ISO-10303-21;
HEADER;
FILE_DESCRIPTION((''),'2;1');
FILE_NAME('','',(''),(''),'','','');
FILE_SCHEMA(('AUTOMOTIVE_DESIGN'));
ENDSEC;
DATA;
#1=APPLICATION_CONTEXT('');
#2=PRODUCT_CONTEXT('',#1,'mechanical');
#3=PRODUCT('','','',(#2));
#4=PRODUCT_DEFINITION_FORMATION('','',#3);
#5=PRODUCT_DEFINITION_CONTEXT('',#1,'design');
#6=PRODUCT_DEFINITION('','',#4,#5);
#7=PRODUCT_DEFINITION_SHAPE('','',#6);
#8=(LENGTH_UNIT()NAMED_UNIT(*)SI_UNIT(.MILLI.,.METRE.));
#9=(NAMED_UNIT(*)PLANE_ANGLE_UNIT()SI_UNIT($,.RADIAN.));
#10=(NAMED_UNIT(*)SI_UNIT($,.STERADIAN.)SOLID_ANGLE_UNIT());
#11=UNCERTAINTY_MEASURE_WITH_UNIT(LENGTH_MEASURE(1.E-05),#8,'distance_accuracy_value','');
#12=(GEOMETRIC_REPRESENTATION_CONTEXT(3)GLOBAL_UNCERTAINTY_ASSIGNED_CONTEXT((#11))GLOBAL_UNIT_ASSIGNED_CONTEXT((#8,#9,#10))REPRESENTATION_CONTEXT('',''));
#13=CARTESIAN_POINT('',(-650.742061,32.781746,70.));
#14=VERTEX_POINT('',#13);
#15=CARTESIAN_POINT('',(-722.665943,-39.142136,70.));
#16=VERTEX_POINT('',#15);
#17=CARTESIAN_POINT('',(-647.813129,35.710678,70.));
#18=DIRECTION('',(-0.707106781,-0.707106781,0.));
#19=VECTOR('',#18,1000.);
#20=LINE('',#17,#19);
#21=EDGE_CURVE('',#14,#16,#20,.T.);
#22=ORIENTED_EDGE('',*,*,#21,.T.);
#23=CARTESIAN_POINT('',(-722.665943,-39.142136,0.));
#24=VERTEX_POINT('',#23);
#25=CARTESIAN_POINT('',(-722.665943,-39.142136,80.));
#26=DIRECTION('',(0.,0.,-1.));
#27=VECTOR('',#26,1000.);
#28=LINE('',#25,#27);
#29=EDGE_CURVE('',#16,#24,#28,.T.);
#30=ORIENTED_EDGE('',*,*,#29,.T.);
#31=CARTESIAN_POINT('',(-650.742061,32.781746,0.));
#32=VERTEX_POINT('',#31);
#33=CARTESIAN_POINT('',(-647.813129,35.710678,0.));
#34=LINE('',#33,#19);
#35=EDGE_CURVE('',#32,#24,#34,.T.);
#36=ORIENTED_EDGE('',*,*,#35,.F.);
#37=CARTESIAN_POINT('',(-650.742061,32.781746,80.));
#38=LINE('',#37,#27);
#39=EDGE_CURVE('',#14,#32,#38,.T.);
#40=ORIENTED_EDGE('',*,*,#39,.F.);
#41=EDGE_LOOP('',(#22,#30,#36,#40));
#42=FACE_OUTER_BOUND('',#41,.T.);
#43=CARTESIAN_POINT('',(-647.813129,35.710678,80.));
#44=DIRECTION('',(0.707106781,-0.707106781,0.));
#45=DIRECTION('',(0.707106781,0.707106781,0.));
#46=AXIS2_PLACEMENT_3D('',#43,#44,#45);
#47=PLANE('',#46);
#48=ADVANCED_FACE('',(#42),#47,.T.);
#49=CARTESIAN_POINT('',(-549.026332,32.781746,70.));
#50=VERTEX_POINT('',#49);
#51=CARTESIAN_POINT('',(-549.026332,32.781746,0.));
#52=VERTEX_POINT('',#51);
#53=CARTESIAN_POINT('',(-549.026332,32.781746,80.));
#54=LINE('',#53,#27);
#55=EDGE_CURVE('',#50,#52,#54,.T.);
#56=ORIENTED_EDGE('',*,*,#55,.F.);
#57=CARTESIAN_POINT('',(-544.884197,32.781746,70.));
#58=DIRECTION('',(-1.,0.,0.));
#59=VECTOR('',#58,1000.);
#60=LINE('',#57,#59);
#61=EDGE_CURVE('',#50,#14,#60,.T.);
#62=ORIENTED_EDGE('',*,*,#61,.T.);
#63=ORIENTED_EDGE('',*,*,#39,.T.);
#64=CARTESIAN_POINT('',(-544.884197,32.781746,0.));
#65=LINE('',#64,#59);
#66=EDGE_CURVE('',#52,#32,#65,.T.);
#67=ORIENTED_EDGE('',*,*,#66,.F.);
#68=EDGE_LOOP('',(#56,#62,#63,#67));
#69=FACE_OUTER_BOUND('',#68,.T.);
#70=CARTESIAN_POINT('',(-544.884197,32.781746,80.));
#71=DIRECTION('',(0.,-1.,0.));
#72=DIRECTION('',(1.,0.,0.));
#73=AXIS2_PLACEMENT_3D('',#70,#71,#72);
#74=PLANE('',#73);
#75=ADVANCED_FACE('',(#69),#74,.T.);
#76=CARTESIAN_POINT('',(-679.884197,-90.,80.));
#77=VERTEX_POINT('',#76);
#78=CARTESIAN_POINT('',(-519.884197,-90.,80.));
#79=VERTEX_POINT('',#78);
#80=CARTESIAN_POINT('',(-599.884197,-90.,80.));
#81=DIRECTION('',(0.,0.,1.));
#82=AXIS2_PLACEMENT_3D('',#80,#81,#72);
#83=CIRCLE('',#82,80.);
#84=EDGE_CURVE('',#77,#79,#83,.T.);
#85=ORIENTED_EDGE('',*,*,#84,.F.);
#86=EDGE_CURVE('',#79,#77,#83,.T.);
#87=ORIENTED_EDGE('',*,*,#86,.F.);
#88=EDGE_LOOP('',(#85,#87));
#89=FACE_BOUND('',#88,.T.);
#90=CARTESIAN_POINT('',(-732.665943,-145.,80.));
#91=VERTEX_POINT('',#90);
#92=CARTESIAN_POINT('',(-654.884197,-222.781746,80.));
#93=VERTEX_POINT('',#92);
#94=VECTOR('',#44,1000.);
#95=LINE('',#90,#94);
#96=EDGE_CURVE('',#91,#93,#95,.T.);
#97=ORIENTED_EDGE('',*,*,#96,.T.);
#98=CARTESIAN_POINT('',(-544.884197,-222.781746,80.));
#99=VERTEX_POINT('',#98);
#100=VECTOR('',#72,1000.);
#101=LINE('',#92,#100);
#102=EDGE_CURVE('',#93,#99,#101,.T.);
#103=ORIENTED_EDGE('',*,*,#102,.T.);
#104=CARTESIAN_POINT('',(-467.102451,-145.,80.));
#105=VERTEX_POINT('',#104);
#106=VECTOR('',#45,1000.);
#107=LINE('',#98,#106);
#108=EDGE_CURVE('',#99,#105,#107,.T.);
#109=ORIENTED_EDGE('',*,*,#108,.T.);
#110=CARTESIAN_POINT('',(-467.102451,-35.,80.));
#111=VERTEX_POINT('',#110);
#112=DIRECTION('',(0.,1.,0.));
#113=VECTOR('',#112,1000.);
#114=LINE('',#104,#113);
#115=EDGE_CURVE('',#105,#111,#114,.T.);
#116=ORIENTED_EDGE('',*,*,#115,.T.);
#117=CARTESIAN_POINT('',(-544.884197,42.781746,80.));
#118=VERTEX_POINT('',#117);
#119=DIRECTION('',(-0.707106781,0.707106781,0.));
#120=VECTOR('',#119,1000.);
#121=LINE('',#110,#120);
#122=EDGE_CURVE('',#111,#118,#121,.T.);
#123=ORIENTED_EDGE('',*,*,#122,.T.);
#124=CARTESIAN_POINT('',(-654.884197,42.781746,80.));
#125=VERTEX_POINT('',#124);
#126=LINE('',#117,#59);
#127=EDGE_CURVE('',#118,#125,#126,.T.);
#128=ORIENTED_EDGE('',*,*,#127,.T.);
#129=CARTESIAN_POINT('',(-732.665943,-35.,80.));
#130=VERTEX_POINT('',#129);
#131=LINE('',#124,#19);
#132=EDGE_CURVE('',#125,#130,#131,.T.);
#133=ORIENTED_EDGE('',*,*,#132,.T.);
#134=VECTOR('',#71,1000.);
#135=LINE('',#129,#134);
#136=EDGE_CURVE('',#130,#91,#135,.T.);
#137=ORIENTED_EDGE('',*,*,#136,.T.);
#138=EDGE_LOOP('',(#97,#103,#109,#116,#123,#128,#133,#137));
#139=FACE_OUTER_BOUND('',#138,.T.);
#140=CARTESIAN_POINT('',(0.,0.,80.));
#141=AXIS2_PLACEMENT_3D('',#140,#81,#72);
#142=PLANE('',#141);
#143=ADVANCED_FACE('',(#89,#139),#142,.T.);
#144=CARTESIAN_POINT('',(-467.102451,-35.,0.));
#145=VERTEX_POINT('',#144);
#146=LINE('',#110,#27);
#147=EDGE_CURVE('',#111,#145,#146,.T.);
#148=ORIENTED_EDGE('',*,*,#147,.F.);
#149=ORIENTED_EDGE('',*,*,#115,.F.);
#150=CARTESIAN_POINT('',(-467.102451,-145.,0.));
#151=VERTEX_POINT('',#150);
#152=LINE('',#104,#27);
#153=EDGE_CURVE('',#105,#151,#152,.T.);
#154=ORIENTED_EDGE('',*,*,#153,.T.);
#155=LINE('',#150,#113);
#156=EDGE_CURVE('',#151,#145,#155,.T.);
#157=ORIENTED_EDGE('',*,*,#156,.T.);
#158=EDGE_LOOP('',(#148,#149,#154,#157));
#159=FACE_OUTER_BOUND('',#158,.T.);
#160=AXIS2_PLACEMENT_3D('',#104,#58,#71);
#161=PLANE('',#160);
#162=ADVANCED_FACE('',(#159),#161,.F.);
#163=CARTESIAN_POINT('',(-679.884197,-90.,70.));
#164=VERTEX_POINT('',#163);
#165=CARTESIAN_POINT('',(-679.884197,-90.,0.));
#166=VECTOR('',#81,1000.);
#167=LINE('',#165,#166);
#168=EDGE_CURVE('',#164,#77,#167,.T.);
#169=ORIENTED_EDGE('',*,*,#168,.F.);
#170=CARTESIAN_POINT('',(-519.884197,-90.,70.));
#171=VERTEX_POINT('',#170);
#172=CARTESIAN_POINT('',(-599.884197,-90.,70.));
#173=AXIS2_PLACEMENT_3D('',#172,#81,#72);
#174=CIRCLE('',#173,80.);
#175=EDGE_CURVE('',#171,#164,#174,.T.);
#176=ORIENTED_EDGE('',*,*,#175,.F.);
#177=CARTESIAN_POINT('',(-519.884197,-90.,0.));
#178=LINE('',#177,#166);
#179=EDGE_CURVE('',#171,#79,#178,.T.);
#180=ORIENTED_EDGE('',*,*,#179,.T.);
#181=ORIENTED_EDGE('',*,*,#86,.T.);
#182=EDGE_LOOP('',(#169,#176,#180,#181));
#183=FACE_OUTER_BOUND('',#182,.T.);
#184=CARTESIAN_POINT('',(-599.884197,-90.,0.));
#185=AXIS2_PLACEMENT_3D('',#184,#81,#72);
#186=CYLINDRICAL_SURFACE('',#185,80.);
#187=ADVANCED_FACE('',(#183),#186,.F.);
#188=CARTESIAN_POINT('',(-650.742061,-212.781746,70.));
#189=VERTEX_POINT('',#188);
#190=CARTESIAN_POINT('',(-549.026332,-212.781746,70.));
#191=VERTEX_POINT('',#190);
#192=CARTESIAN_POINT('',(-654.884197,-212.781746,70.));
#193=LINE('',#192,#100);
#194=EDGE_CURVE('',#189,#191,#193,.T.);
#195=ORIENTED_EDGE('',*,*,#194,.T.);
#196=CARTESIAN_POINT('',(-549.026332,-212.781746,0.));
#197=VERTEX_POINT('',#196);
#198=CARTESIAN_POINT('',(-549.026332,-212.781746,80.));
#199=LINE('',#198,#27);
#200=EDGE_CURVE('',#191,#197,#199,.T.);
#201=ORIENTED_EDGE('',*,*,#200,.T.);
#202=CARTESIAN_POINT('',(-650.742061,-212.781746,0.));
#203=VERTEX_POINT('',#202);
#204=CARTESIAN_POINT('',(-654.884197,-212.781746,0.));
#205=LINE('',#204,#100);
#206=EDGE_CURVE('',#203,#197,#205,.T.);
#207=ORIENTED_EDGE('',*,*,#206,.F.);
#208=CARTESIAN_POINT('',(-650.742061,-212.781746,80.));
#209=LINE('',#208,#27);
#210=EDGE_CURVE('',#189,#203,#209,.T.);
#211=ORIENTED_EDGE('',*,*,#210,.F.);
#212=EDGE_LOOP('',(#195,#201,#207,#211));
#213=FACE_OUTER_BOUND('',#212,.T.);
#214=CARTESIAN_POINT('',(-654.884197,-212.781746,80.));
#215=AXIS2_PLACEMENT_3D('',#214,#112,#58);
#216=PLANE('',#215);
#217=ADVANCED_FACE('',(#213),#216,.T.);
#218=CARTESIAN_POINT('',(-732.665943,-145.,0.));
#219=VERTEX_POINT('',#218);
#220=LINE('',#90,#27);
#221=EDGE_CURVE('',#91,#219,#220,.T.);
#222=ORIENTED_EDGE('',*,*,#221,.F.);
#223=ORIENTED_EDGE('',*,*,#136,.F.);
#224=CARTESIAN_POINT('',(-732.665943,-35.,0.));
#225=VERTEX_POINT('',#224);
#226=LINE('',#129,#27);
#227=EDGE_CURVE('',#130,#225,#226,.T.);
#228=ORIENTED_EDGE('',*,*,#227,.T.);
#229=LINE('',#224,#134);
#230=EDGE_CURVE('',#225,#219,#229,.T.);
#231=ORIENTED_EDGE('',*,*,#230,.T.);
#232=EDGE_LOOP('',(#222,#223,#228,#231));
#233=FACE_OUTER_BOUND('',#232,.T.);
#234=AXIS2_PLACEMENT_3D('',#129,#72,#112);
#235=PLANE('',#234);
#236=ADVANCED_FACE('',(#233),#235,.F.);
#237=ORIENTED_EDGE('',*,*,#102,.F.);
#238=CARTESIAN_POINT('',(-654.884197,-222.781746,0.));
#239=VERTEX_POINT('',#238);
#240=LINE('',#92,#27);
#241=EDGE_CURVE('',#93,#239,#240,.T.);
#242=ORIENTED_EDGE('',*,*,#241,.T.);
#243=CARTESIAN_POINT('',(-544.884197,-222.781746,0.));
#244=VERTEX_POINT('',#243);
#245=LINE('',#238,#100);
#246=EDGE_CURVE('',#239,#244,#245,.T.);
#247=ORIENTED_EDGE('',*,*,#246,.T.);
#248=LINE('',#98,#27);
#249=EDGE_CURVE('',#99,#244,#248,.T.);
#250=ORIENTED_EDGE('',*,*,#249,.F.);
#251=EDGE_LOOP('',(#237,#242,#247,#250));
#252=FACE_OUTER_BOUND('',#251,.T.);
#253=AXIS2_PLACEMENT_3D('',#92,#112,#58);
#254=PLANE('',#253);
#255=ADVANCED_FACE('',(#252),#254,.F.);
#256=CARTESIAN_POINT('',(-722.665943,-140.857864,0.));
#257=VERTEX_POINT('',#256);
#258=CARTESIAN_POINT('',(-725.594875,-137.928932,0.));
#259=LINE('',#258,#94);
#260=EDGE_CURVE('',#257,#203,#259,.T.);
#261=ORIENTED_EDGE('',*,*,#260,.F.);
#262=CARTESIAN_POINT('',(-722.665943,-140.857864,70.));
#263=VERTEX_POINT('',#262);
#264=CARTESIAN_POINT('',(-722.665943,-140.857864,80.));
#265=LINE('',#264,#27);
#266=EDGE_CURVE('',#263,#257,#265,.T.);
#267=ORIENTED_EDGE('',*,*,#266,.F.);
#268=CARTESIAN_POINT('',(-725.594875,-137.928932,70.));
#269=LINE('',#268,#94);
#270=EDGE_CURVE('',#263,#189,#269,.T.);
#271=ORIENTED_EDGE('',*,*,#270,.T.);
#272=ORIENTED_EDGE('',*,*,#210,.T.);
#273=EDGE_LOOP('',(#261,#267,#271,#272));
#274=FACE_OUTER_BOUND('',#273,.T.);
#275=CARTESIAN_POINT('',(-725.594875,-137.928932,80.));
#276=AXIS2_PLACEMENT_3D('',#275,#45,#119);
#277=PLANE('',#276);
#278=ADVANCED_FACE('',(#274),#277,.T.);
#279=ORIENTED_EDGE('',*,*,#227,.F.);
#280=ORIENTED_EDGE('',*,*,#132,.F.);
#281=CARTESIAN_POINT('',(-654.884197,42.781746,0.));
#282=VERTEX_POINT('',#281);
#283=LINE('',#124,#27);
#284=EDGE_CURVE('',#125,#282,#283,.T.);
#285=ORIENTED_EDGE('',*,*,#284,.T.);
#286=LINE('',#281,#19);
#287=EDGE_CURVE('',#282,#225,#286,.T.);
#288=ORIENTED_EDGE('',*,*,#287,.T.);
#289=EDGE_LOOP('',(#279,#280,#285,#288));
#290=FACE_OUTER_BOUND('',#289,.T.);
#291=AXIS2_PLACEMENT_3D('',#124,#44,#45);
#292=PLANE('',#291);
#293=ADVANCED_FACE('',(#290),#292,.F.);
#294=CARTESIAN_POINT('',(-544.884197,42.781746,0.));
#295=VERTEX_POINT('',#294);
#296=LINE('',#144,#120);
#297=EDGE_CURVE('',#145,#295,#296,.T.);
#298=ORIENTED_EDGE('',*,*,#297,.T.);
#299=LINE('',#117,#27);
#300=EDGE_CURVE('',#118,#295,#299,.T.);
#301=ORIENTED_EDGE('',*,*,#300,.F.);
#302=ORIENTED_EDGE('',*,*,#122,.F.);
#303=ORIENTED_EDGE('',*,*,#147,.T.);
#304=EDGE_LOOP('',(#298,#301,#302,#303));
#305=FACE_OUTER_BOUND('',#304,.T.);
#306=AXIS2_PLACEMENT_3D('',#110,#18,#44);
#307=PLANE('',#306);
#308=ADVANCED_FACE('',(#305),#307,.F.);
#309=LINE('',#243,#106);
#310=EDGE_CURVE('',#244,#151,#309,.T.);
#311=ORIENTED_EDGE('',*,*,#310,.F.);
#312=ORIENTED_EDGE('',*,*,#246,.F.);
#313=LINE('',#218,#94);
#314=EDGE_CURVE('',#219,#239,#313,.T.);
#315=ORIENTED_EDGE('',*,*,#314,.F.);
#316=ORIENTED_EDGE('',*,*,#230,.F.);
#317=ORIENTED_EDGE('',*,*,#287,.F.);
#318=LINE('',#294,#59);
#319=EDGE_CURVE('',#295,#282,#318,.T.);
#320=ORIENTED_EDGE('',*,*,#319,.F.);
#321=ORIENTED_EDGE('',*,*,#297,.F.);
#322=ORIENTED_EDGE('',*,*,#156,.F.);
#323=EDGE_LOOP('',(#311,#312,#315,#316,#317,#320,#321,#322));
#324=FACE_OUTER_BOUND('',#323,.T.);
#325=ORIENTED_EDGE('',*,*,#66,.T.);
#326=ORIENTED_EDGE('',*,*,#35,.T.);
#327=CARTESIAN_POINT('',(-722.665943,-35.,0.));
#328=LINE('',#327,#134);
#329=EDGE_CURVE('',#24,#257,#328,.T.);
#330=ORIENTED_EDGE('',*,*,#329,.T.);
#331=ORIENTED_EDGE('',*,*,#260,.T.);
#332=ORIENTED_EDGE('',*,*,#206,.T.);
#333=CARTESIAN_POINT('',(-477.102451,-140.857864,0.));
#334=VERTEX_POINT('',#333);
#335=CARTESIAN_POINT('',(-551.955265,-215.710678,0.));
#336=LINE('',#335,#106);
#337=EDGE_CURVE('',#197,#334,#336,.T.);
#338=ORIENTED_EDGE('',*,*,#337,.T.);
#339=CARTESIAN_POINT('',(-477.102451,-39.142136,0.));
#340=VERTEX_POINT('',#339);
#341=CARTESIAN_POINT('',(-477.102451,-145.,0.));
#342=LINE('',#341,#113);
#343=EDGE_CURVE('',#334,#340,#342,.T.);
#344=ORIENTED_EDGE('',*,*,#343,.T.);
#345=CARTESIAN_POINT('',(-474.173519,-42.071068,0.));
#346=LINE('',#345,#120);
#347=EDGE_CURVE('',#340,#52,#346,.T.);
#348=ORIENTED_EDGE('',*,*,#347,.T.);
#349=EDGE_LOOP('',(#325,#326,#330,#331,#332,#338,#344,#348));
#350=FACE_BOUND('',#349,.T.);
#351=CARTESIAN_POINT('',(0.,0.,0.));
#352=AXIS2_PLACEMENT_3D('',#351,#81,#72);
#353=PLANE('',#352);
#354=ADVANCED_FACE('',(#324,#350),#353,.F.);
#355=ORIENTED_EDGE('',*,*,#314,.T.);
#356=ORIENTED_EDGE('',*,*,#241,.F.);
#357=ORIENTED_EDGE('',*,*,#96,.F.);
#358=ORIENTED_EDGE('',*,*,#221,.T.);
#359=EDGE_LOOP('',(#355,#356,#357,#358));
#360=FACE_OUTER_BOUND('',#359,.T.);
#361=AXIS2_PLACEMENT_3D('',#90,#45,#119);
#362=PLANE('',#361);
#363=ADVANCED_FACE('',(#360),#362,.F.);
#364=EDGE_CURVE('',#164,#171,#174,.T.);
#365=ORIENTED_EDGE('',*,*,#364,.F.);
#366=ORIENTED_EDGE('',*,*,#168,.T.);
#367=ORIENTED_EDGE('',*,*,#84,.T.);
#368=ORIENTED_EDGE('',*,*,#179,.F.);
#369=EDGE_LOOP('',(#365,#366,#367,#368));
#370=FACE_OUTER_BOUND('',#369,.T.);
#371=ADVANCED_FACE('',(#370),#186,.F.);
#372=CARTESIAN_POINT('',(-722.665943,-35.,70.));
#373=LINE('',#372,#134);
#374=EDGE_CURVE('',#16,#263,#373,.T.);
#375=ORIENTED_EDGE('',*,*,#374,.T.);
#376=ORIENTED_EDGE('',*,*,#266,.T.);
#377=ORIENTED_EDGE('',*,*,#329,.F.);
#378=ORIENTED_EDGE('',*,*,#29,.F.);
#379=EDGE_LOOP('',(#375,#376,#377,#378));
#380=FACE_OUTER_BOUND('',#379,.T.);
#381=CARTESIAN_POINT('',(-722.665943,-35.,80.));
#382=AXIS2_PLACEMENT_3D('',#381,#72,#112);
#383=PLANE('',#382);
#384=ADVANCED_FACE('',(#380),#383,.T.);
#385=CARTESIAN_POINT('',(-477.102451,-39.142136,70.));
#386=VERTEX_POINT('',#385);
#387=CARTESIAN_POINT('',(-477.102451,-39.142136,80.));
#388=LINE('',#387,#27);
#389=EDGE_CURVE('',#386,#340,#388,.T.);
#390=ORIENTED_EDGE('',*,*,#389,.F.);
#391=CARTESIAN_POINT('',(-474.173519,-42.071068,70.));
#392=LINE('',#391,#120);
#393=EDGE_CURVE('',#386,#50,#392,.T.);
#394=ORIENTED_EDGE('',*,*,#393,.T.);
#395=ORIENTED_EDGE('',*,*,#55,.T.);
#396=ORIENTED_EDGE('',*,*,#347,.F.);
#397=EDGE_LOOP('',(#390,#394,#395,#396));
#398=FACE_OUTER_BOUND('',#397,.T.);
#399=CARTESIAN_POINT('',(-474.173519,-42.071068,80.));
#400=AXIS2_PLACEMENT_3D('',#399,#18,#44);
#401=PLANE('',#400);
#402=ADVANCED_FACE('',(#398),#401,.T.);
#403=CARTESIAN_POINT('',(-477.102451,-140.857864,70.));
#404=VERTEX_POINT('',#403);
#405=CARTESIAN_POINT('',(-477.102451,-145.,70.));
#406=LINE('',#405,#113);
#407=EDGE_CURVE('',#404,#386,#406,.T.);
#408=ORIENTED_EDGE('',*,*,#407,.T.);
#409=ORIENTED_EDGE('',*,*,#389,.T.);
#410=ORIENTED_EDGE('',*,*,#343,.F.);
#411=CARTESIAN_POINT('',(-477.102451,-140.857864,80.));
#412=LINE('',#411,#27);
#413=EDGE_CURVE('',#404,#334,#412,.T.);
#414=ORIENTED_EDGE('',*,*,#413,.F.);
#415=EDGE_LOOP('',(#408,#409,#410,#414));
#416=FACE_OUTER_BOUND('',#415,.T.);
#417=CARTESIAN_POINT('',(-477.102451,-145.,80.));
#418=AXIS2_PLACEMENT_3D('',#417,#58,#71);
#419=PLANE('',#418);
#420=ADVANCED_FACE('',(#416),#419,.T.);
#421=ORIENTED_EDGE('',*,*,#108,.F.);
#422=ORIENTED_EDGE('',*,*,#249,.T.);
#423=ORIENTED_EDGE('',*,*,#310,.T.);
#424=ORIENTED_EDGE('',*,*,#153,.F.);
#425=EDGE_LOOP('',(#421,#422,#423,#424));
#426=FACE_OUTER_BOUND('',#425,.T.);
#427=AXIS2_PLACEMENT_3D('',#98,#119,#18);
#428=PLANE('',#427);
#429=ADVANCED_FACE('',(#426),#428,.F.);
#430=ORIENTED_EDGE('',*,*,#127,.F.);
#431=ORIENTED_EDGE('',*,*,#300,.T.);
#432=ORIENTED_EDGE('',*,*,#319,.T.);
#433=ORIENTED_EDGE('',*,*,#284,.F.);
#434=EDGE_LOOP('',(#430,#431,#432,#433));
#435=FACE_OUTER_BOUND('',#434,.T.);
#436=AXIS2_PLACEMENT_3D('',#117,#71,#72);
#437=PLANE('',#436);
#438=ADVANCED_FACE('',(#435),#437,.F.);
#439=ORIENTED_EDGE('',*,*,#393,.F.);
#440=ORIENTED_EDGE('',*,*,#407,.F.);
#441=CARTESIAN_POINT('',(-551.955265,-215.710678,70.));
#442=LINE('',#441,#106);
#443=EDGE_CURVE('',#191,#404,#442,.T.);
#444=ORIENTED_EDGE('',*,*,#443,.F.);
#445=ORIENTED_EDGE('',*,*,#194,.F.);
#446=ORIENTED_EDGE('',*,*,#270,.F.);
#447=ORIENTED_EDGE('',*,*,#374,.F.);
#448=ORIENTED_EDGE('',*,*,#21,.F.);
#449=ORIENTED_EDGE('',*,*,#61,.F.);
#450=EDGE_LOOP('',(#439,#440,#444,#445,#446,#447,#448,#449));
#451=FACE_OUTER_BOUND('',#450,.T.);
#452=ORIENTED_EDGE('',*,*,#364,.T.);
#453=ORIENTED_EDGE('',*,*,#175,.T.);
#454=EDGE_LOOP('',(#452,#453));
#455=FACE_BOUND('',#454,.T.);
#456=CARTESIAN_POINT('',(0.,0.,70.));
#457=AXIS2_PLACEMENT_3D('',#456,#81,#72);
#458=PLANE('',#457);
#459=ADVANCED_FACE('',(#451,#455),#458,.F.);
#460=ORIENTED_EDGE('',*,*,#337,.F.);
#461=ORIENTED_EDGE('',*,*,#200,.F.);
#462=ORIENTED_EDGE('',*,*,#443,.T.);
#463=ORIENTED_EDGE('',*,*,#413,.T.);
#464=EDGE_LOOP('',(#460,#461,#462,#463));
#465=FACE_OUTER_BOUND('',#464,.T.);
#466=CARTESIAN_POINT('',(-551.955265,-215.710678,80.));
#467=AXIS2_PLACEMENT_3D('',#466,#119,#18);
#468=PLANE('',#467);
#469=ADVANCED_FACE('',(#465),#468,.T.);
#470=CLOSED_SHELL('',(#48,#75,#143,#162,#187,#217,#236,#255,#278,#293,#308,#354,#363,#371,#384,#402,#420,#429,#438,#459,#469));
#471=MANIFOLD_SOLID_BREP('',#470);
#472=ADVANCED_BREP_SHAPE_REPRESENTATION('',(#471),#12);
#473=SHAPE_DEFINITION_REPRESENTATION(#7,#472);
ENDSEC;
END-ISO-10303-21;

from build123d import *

# Parameters (mm, degrees)
BOSS_EXTRUDE1_DEPTH = 80
SHELL1_T            = -10
SKETCH2_R           = 80
CUT_EXTRUDE1_DEPTH  = 80


with BuildPart() as part:
    # Sketch1 → Boss-Extrude1 (new body)
    with BuildSketch(Plane.XY):
        Polygon((-467.102450828, -35), (-544.884196758, 42.781745931), (-654.884196758, 42.781745931), (-732.665942689, -35), (-732.665942689, -145), (-654.884196758, -222.781745931), (-544.884196758, -222.781745931), (-467.102450828, -145), align=None)
    extrude(amount=BOSS_EXTRUDE1_DEPTH)

    # Shell1
    shell1_openings = [part.faces().sort_by_distance(p)[0] for p in [
        (-599.884196758, -90, 0),
    ]]
    offset(amount=SHELL1_T, openings=shell1_openings, kind=Kind.INTERSECTION)

    # Sketch2 → Cut-Extrude1 (cut)
    with BuildSketch(Plane.XY.offset(80)):
        with Locations((-599.884196758, -90)):
            Circle(SKETCH2_R)
    extrude(amount=-CUT_EXTRUDE1_DEPTH, mode=Mode.SUBTRACT)


solid = part.part
